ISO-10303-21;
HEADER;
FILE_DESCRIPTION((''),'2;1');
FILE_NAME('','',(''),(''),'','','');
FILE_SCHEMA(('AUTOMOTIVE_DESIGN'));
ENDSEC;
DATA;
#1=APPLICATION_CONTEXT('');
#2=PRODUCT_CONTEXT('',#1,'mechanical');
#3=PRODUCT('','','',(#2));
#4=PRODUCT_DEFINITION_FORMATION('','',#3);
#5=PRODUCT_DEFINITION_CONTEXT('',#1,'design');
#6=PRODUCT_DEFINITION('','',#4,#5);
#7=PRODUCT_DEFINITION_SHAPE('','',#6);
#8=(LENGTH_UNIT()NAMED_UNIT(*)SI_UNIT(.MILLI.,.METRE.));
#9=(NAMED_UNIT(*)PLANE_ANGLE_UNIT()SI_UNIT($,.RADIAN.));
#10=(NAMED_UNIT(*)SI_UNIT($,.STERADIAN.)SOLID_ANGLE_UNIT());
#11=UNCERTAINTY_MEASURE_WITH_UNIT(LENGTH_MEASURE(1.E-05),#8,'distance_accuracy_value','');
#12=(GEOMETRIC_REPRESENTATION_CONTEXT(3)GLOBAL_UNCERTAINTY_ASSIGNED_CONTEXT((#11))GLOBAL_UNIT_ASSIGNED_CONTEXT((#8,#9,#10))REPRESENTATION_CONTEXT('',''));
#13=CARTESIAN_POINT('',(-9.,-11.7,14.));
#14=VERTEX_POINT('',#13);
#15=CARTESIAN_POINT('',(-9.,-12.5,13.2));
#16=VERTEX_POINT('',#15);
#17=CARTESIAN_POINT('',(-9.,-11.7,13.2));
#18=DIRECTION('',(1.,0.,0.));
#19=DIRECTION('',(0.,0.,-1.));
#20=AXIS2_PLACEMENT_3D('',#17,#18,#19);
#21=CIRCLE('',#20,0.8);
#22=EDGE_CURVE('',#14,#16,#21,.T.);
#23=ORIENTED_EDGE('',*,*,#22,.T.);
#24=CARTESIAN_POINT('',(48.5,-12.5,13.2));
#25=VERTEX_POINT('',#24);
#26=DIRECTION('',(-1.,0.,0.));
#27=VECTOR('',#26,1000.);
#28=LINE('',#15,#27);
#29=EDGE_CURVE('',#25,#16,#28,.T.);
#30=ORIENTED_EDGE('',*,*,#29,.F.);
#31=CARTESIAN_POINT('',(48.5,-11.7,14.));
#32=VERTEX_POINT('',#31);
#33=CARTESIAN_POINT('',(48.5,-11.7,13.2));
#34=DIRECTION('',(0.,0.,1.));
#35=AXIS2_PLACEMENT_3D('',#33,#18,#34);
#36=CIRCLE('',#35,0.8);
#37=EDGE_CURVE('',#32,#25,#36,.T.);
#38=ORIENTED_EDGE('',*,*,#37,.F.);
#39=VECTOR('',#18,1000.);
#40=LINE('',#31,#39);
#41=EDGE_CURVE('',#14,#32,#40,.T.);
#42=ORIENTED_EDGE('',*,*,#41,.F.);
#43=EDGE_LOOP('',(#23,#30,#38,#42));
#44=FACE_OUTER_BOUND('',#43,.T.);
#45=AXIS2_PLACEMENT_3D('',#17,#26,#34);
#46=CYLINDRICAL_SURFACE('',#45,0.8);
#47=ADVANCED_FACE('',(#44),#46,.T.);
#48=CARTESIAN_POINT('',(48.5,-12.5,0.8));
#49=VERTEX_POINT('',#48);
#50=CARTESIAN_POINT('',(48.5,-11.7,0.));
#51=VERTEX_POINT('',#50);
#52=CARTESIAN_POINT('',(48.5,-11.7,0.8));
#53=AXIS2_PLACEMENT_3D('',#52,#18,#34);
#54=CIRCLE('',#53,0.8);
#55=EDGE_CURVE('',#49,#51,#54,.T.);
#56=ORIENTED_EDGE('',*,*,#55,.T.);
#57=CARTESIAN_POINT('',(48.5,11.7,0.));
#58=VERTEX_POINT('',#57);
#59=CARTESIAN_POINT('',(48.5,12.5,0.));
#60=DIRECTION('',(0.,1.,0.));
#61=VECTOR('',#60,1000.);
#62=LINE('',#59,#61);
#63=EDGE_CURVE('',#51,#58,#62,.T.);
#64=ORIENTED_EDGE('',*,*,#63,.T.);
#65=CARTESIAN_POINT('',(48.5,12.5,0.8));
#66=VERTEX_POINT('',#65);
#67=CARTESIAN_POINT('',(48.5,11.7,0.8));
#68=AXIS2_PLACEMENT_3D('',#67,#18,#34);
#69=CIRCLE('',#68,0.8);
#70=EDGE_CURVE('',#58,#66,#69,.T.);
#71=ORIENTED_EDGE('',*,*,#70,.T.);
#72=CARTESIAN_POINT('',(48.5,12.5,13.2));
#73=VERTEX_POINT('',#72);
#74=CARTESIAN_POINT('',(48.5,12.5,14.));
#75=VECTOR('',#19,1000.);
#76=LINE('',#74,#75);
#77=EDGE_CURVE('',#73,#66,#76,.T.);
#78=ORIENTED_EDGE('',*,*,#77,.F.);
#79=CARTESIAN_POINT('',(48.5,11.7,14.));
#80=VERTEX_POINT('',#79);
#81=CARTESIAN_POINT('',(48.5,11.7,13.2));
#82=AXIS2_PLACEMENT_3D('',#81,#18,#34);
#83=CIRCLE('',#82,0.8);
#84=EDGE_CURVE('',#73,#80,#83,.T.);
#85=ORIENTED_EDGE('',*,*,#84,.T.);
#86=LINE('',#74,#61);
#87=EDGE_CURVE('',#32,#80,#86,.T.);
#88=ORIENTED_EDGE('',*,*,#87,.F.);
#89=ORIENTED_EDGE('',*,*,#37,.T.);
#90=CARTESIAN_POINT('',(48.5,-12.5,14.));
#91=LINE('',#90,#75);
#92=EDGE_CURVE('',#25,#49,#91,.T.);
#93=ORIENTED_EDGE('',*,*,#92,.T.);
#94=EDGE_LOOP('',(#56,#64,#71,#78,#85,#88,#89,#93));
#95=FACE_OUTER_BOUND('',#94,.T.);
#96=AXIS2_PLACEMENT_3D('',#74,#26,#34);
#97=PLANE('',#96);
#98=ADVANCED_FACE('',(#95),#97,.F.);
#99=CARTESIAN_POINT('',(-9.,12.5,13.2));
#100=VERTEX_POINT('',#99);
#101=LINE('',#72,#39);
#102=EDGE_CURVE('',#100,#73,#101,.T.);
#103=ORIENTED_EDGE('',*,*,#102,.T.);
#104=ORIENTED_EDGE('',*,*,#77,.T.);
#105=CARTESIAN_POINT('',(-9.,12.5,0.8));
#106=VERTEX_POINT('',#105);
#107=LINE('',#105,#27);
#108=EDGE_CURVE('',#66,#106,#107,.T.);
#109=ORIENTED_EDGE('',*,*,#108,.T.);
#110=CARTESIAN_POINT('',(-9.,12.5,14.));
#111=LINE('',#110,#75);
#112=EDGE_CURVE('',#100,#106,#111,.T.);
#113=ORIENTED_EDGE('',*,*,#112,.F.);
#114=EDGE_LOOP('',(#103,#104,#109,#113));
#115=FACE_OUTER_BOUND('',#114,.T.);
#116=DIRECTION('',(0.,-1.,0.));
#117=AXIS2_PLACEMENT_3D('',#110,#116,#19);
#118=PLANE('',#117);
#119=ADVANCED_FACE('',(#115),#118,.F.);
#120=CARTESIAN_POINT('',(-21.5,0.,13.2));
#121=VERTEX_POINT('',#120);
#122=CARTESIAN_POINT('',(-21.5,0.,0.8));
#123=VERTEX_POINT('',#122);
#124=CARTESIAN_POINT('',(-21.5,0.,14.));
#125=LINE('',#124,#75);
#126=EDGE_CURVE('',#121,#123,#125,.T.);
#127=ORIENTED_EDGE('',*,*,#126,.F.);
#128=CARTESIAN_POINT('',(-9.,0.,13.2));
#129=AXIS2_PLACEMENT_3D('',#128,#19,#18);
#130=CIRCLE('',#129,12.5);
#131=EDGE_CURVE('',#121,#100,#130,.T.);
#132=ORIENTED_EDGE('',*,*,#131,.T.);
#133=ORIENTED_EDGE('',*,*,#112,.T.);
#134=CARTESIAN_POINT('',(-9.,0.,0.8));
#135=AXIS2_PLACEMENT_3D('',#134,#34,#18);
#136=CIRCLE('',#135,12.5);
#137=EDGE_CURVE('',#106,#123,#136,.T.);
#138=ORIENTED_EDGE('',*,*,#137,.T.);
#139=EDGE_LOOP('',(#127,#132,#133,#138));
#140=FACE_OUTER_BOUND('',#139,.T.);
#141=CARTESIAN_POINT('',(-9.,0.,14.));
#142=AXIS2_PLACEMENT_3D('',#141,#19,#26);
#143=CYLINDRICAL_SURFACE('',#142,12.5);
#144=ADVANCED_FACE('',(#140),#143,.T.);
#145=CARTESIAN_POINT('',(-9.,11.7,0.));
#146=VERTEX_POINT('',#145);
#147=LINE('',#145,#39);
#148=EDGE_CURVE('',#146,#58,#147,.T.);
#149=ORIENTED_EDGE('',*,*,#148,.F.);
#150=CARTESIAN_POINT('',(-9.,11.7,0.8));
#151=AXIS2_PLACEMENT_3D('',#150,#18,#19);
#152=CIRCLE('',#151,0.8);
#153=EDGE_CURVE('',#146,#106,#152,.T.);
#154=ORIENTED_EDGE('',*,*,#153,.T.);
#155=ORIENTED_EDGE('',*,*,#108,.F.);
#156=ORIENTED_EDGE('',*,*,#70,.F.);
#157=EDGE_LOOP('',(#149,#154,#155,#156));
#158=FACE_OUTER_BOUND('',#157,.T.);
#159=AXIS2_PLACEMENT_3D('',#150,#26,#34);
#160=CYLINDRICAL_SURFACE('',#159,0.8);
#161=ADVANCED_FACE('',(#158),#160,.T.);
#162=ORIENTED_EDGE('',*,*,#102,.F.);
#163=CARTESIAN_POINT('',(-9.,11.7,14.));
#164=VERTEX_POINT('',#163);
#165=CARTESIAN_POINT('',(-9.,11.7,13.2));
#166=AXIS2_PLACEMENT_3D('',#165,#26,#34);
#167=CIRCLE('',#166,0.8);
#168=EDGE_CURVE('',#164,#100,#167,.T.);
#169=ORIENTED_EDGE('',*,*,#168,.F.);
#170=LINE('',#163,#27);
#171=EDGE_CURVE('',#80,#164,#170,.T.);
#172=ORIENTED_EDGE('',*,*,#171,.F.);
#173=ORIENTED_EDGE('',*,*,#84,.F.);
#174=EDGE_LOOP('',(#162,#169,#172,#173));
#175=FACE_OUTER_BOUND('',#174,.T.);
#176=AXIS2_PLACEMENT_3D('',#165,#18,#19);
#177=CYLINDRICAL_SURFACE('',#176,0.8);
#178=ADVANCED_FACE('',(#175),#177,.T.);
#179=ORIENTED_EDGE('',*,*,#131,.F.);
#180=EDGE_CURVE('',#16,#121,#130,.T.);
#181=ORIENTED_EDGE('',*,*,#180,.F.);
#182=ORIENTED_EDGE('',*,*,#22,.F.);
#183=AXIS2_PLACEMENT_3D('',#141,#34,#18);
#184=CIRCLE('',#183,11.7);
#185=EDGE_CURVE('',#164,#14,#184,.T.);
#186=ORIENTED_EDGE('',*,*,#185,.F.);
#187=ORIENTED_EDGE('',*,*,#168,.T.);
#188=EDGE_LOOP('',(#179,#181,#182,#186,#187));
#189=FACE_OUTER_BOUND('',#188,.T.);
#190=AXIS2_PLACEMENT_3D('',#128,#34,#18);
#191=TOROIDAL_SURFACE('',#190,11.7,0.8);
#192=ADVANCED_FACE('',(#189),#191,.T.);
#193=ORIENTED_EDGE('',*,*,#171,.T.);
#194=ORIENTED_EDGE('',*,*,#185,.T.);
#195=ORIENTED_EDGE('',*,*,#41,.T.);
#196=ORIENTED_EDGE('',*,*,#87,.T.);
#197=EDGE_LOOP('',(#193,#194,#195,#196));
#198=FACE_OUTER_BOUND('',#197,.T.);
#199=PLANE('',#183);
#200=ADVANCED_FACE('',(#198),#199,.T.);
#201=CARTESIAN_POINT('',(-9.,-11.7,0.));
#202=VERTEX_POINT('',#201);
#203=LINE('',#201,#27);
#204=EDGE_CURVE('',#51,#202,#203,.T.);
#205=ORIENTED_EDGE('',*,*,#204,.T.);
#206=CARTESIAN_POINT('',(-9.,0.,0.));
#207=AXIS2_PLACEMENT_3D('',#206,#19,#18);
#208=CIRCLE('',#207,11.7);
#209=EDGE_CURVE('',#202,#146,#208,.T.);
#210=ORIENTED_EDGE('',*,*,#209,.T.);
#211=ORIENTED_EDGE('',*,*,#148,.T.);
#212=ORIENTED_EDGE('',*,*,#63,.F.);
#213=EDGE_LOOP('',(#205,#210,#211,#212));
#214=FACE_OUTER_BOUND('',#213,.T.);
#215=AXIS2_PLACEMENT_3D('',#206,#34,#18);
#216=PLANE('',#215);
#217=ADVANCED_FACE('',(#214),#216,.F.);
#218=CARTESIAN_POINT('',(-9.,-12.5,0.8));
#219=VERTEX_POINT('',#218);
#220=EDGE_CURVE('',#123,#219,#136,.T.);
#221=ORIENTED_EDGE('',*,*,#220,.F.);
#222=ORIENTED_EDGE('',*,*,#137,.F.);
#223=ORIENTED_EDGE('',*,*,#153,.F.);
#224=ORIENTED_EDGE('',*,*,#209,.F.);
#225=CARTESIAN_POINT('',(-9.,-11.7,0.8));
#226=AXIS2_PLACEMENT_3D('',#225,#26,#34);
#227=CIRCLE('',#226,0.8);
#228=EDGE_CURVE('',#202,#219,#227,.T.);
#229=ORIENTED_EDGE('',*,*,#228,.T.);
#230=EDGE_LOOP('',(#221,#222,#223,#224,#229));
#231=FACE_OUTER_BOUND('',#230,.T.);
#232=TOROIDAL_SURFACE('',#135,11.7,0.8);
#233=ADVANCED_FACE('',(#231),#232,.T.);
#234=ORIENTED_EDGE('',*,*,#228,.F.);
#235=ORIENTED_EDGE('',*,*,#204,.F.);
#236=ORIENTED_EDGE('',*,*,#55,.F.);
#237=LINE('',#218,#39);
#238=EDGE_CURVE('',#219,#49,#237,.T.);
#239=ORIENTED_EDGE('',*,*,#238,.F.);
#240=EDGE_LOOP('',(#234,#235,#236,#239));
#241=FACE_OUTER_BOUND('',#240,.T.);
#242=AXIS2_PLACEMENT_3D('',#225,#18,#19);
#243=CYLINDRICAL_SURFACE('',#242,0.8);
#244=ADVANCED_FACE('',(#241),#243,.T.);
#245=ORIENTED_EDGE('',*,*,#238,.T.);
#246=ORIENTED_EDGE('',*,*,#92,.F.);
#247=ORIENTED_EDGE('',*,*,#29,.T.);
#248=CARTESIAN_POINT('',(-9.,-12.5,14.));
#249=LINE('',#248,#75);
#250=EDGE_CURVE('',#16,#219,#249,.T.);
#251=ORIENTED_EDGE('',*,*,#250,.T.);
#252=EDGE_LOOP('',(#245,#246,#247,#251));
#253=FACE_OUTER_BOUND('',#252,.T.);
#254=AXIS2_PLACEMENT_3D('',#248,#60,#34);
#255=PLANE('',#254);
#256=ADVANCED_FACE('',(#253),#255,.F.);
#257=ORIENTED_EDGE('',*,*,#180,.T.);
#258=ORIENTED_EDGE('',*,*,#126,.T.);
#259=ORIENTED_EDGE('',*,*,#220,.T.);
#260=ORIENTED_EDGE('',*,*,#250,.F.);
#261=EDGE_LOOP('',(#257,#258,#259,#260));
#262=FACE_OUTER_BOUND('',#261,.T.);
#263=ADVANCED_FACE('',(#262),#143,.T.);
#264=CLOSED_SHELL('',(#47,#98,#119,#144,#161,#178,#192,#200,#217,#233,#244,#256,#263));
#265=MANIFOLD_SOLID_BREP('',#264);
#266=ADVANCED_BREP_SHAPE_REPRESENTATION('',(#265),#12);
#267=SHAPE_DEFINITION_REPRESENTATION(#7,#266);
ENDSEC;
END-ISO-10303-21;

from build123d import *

# Parameters (mm, degrees)
EXTRUDE_494_DEPTH = 14
FILLET_1_R        = 0.8


with BuildPart() as part:
    # 草图1 → Extrude 494 (new body)
    with BuildSketch(Plane.XY):
        with BuildLine():
            Line((-9, 12.5), (48.5, 12.5))
            Line((48.5, 12.5), (48.5, -12.5))
            Line((48.5, -12.5), (-9, -12.5))
            ThreePointArc((-9, -12.5), (-21.5, 0), (-9, 12.5))
        make_face()
    extrude(amount=EXTRUDE_494_DEPTH)

    # 圆角1
    fillet_1_edges = [part.edges().sort_by_distance(p)[0] for p in [
        (-21.5, 0, 14),
        (19.75, -12.5, 14),
        (19.75, -12.5, 0),
        (-21.5, 0, 0),
        (19.75, 12.5, 0),
        (19.75, 12.5, 14),
    ]]
    fillet(fillet_1_edges, radius=FILLET_1_R)


solid = part.part
